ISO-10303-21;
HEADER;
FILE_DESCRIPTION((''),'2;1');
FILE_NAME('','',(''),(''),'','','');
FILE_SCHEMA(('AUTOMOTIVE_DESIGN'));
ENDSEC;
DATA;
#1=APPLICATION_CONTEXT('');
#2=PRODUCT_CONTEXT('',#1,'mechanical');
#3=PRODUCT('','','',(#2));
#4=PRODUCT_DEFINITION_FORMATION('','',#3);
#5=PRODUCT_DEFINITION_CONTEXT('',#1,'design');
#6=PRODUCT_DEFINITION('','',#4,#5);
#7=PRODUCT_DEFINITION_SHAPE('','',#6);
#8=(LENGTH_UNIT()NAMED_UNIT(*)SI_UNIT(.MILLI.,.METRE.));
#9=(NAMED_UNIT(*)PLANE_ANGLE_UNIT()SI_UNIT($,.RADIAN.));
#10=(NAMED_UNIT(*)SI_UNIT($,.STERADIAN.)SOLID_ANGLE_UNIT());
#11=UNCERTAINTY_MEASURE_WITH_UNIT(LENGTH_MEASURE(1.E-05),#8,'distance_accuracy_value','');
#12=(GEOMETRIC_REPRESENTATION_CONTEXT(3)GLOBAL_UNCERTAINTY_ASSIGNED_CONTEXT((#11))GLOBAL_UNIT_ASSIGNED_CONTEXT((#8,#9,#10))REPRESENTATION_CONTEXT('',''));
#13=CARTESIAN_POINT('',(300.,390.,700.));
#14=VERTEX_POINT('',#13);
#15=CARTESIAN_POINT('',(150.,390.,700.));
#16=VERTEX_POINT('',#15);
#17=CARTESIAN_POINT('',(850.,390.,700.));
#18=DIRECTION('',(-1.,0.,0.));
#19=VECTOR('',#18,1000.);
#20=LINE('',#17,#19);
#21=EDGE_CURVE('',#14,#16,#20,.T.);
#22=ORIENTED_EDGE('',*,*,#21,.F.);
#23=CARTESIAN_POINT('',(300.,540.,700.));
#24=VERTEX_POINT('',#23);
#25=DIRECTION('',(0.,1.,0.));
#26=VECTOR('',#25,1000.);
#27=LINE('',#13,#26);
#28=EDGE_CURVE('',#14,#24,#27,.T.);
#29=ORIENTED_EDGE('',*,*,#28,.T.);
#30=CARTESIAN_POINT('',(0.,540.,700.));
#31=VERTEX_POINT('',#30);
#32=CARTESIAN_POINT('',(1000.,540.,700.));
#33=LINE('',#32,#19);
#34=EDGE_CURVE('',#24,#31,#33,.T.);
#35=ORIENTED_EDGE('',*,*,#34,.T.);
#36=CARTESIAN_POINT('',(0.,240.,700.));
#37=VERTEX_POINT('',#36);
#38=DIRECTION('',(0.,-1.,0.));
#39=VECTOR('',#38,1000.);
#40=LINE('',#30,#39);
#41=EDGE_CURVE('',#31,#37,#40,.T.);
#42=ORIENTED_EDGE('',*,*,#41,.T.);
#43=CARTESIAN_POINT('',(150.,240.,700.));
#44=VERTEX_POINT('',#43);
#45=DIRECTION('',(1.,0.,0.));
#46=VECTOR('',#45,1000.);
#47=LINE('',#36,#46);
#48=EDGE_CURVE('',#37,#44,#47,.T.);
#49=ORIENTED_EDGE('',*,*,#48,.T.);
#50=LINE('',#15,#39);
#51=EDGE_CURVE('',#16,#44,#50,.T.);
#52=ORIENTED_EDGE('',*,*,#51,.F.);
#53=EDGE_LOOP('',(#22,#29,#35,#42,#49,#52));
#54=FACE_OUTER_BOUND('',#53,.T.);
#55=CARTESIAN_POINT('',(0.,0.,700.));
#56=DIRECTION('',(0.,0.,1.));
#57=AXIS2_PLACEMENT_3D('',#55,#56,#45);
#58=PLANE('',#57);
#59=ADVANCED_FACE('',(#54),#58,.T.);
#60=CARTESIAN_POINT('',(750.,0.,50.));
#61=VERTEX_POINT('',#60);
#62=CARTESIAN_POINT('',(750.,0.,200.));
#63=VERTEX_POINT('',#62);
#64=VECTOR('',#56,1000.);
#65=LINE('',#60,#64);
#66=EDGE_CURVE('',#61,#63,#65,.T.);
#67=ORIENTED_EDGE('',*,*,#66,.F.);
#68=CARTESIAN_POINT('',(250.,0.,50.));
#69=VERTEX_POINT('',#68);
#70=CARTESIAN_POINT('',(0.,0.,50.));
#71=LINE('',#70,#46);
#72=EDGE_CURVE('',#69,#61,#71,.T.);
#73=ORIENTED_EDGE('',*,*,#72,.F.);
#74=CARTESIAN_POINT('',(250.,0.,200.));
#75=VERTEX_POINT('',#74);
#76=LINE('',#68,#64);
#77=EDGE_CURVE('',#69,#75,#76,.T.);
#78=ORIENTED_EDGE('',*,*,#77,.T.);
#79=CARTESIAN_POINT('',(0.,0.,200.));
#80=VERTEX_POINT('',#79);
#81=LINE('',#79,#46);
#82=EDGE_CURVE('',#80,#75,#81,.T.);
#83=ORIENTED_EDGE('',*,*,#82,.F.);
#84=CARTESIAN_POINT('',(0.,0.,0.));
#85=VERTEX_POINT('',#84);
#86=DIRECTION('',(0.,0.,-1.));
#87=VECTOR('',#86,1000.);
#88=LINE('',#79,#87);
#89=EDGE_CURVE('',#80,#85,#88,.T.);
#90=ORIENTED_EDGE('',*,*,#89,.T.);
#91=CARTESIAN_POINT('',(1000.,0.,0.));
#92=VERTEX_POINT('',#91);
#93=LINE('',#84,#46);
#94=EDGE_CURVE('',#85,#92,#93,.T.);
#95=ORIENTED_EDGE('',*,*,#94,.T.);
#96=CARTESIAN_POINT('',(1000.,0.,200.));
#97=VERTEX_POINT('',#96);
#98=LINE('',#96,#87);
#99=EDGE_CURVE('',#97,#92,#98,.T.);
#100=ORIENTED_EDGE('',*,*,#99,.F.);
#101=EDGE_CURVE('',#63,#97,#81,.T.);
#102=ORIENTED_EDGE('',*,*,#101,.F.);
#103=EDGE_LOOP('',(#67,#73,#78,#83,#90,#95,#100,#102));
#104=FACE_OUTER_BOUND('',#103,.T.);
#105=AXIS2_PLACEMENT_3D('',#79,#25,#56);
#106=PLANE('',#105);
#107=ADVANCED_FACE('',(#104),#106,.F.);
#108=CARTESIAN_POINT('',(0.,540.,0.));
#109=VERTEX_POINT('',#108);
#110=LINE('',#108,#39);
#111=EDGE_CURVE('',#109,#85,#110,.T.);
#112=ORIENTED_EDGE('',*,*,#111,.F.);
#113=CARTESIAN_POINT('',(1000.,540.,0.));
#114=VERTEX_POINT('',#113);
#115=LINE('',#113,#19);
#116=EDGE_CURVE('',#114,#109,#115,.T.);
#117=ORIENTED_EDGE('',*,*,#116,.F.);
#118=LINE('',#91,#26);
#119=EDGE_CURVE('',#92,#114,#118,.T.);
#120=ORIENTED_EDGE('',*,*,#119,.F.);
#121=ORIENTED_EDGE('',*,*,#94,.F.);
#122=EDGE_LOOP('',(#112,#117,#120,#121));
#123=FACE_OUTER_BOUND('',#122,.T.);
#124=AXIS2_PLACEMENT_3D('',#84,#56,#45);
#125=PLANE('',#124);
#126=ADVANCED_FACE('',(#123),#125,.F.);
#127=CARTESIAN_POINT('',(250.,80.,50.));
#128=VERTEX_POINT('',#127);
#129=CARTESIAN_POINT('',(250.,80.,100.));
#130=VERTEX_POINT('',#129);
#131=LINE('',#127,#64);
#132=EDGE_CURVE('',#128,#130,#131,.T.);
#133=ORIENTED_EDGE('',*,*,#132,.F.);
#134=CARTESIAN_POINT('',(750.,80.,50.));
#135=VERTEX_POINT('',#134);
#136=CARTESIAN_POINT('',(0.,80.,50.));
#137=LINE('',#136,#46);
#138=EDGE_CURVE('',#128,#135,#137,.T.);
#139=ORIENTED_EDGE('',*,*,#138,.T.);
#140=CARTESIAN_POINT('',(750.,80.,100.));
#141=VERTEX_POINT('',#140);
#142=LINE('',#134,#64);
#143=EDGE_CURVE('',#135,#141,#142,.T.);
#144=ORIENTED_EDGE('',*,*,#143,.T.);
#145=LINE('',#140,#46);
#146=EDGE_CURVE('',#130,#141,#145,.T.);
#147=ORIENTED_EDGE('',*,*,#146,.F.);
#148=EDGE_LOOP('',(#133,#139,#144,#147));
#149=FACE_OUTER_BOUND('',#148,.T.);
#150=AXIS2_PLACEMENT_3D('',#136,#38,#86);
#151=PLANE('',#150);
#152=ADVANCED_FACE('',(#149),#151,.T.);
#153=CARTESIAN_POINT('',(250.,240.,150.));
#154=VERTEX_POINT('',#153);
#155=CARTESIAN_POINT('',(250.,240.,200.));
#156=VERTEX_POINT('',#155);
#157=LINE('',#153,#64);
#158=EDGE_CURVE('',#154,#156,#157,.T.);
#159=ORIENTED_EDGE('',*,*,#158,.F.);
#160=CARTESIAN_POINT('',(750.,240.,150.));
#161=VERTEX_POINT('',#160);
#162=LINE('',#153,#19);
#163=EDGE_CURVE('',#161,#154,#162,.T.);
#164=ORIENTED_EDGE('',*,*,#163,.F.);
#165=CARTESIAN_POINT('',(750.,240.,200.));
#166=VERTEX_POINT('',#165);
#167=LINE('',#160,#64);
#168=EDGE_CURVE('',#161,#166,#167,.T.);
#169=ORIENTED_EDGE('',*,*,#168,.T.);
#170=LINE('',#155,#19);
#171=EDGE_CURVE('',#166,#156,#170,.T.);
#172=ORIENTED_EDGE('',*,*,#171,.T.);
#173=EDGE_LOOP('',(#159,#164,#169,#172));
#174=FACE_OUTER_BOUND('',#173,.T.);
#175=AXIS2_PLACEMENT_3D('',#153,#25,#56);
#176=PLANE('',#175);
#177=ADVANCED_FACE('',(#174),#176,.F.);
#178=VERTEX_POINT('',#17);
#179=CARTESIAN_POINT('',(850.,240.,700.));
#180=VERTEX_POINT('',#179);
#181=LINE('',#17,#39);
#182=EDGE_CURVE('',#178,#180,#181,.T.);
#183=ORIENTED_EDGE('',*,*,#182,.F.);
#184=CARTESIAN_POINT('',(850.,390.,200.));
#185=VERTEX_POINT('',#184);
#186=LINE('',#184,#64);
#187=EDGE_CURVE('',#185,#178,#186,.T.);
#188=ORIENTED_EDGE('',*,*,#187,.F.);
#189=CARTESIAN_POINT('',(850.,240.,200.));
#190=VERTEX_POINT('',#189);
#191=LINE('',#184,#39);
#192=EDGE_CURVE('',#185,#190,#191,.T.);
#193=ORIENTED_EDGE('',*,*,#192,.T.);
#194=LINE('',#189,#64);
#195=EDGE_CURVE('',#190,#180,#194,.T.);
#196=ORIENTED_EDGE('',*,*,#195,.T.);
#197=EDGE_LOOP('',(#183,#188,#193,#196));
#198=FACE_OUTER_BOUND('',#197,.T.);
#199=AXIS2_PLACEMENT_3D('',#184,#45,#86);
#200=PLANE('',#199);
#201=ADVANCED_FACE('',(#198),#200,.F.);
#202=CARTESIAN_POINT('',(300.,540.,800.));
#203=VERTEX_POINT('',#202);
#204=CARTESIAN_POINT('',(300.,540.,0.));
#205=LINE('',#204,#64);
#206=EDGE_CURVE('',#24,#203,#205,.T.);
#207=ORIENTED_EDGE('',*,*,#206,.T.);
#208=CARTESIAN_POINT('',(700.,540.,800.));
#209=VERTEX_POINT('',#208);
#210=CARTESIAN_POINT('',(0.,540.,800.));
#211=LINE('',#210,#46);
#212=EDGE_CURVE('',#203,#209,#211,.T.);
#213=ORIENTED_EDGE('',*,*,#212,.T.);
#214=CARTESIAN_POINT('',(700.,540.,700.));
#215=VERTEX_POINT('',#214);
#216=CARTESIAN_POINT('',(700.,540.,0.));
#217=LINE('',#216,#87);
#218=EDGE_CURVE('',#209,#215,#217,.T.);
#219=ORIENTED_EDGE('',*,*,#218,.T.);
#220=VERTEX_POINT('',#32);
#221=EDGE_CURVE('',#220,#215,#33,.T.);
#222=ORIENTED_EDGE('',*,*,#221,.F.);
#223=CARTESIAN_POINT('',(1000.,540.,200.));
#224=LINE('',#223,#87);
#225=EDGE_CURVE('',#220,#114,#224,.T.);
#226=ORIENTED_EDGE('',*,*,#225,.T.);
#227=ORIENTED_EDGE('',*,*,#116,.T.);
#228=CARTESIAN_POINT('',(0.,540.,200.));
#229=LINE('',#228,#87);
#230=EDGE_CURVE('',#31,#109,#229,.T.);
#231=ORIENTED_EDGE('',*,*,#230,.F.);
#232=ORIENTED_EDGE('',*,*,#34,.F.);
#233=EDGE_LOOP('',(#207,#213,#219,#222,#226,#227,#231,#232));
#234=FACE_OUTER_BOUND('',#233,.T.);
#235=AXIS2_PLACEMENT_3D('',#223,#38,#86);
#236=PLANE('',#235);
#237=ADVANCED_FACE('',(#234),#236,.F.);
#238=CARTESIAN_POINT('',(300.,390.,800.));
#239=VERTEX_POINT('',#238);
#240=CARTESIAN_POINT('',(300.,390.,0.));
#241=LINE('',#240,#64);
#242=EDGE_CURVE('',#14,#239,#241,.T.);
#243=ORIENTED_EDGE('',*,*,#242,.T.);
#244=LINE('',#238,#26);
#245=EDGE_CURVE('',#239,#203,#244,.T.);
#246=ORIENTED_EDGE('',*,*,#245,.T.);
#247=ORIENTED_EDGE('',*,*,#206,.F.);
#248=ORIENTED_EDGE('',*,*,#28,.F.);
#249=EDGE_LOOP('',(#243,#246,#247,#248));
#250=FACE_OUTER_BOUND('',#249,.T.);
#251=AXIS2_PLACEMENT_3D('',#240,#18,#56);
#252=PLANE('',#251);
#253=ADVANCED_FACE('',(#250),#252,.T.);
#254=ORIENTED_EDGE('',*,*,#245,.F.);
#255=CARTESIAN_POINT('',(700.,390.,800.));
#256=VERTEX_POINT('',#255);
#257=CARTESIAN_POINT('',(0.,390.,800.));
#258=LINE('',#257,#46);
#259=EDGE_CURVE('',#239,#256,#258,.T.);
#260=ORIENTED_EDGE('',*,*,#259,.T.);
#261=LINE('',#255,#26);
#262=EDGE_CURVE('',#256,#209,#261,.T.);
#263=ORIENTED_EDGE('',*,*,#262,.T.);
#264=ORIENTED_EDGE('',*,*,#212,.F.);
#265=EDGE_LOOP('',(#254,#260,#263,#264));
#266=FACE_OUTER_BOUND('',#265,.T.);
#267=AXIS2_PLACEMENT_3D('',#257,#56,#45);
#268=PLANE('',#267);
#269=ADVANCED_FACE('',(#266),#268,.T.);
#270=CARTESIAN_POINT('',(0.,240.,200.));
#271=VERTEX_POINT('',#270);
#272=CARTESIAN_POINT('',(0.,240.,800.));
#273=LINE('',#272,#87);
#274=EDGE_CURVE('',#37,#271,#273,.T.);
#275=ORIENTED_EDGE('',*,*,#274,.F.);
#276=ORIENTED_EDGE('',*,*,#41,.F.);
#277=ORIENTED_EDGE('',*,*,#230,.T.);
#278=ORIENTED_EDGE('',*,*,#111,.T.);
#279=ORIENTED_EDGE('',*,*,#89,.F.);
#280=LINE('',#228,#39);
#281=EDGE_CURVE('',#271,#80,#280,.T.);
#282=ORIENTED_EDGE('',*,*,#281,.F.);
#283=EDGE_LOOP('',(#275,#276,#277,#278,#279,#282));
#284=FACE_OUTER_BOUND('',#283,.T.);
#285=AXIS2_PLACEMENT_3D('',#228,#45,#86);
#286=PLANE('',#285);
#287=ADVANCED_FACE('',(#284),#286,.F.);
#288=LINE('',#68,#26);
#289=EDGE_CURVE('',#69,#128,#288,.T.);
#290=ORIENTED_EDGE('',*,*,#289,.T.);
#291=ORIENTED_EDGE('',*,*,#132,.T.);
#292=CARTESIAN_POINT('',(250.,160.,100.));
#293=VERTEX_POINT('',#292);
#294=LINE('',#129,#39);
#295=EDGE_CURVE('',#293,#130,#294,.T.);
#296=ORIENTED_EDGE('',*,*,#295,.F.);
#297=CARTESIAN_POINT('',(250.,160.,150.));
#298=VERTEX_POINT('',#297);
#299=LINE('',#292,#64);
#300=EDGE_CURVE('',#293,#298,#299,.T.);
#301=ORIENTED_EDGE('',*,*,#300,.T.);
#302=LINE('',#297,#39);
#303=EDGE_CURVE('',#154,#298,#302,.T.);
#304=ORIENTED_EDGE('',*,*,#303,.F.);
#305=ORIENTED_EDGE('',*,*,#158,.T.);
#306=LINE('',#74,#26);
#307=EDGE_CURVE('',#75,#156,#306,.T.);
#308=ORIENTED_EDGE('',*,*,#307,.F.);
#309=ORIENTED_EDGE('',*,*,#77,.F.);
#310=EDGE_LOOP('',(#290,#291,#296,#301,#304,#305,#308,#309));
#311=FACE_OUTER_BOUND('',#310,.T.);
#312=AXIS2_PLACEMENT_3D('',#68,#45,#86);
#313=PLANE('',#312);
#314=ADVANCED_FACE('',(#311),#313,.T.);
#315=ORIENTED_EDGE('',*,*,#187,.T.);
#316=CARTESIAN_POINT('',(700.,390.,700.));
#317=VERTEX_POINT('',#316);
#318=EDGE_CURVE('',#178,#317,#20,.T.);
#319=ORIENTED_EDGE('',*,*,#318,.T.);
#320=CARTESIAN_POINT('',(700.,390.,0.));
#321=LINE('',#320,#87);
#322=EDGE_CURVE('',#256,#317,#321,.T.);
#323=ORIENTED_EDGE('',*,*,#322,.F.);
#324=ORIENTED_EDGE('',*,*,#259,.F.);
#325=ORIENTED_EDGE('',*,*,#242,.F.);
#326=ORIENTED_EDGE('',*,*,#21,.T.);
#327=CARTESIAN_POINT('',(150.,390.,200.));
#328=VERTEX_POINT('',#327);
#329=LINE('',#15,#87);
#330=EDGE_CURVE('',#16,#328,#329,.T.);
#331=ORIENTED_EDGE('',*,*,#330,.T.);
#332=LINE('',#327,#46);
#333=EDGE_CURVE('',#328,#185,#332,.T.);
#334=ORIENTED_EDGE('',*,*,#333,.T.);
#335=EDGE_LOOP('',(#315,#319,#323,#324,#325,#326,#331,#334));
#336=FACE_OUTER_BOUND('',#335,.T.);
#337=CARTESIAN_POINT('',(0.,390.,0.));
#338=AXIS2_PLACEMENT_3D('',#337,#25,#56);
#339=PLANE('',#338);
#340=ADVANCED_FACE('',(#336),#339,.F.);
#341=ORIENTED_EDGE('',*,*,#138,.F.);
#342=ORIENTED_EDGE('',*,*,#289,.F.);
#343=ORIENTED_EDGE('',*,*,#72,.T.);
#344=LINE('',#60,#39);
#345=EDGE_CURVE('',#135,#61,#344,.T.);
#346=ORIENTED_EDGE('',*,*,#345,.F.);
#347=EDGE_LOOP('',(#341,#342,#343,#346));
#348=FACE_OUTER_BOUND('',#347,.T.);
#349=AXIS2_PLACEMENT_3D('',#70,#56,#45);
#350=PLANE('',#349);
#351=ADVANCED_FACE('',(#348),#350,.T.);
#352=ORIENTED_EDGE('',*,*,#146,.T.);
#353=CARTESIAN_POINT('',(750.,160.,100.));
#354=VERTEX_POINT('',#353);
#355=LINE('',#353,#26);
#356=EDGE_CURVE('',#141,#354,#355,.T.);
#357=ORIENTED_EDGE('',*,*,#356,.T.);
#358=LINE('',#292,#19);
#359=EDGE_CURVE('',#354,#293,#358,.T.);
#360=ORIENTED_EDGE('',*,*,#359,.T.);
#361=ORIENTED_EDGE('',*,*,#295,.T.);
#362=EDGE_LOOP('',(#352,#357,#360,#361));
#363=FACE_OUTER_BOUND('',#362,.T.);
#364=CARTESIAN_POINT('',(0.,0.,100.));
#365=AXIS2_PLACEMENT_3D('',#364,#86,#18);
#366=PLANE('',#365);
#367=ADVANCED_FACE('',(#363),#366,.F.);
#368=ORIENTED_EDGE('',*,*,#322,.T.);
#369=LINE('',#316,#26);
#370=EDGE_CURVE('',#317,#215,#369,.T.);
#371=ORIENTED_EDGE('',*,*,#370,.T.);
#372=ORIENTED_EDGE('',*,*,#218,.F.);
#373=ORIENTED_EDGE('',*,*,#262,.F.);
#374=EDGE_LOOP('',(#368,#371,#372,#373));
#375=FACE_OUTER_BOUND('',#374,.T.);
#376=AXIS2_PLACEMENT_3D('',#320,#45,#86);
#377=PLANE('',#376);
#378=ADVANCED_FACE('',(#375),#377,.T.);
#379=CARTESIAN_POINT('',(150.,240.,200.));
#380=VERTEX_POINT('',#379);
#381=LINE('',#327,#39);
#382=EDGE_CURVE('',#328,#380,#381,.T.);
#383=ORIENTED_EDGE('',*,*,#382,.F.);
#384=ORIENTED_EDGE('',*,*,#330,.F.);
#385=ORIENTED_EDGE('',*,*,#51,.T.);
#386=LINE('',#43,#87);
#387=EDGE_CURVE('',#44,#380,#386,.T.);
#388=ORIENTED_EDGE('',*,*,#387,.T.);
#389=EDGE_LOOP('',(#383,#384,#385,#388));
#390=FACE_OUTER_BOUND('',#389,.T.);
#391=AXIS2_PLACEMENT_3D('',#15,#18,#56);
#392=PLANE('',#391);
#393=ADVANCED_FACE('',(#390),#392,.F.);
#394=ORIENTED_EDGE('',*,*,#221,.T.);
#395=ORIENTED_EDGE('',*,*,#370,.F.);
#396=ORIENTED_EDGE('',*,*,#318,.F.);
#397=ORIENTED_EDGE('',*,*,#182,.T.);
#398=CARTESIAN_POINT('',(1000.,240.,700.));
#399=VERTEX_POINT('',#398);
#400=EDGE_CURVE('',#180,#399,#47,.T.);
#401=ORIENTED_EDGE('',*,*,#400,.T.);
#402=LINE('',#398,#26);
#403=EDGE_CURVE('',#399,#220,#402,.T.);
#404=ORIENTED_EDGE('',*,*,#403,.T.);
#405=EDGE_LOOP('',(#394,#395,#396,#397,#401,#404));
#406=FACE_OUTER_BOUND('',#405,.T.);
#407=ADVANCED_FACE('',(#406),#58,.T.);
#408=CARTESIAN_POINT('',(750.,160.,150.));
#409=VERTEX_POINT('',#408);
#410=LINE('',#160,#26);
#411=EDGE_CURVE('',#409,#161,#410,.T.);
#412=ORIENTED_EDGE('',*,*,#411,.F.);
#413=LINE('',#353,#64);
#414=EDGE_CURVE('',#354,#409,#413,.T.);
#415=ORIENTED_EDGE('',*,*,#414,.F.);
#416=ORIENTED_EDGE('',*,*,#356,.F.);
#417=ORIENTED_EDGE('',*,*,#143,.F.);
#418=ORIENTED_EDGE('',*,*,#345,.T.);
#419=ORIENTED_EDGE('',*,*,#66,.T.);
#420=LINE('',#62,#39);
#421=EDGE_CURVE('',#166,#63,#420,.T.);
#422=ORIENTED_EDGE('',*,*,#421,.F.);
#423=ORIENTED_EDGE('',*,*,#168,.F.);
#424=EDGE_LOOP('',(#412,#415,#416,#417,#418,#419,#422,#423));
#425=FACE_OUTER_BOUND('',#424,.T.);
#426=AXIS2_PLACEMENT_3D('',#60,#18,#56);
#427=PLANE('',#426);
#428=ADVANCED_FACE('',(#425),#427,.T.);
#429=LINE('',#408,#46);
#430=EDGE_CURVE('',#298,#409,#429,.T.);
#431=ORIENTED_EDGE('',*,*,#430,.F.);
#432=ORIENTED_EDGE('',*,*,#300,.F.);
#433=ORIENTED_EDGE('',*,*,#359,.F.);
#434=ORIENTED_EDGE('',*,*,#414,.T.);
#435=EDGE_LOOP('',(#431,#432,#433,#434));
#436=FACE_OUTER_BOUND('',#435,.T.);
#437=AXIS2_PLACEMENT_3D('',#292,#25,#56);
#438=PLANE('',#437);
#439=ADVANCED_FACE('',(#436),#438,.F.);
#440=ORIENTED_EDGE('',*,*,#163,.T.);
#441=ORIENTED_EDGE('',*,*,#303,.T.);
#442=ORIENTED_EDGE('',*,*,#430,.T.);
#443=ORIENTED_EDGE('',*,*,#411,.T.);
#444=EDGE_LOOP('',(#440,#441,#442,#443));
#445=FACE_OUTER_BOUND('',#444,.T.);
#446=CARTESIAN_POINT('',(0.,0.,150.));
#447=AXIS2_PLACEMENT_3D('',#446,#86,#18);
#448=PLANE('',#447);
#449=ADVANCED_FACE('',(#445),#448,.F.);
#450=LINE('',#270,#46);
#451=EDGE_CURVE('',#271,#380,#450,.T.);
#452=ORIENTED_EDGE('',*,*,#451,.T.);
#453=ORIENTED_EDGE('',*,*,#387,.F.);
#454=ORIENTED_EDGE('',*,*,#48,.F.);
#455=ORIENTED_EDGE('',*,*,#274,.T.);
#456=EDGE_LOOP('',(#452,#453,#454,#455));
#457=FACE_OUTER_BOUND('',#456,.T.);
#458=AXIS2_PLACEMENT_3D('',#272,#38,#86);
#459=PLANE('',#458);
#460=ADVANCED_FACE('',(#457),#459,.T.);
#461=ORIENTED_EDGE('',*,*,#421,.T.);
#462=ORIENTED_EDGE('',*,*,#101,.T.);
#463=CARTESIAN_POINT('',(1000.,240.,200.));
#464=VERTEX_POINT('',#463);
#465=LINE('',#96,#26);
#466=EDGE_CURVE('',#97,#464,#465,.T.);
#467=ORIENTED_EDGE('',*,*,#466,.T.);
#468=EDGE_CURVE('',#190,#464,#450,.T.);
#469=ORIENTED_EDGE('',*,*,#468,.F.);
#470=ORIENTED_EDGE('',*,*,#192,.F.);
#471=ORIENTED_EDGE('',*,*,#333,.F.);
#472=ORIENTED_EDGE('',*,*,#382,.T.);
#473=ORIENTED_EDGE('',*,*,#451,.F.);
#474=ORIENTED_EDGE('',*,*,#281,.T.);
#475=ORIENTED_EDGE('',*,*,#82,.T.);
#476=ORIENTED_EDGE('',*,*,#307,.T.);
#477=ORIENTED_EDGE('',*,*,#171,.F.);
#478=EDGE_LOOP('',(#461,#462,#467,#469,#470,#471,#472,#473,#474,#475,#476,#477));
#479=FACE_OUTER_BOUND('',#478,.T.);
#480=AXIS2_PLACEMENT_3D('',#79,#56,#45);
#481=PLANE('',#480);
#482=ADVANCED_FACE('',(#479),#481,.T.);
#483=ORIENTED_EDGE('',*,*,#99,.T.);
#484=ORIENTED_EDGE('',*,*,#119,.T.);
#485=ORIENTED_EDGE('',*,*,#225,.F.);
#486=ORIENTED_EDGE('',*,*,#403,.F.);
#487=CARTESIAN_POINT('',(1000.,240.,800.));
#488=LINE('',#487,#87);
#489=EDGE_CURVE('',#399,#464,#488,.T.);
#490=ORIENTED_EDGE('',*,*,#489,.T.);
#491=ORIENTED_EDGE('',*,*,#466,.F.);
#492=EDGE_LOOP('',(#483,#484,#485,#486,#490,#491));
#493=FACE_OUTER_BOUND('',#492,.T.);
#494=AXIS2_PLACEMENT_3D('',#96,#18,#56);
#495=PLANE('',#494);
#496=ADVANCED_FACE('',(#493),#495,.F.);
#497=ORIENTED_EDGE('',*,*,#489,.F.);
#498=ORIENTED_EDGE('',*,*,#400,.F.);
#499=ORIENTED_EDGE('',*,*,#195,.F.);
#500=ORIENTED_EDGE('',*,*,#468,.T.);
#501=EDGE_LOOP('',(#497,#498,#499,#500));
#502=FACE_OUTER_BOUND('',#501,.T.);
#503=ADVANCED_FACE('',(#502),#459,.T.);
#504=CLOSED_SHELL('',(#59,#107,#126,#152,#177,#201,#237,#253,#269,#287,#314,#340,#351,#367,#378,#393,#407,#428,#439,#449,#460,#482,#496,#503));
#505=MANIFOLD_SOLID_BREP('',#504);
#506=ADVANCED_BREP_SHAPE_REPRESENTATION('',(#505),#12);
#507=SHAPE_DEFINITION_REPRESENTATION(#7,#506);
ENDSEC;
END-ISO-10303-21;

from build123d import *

# Parameters (mm, degrees)
BASE_BLOCK_PROFILE_W            = 1000
BASE_BLOCK_PROFILE_H            = 540
BASE_BLOCK_DEPTH                = 200
RAISED_BLOCK_PROFILE_W          = 600
RAISED_BLOCK_PROFILE_H          = 300
RAISED_BLOCK_DEPTH              = 1000
RAISED_BLOCK_STEP_CUT_PROFILE_W = 1000
RAISED_BLOCK_STEP_CUT_PROFILE_H = 300
RAISED_BLOCK_STEP_CUT_DEPTH     = 100
STAIR_STEP_BOSS_PROFILE_W       = 200
STAIR_STEP_BOSS_PROFILE_H       = 100
STAIR_STEP_BOSS_DEPTH           = 150
STAIR_CUTOUT_DEPTH              = 150
STEPPED_SLOT_PROFILE_W          = 250
STEPPED_SLOT_PROFILE_H          = 80
STEPPED_SLOT_CUT_DEPTH          = 150
SLOT_SECOND_STEP_PROFILE_W      = 500
SLOT_SECOND_STEP_PROFILE_H      = 80
SLOT_SECOND_STEP_CUT_DEPTH      = 100
SLOT_THIRD_STEP_PROFILE_W       = 500
SLOT_THIRD_STEP_PROFILE_H       = 80
SLOT_THIRD_STEP_CUT_DEPTH       = 50


with BuildPart() as part:
    # Base Block Profile → Base Block (new body)
    with BuildSketch(Plane.XY):
        with Locations((500, 270)):
            Rectangle(BASE_BLOCK_PROFILE_W, BASE_BLOCK_PROFILE_H)
    extrude(amount=BASE_BLOCK_DEPTH)

    # Raised Block Profile → Raised Block (add)
    with BuildSketch(Plane(origin=(1000, 0, 0), x_dir=(0, 0, -1), z_dir=(1, 0, 0))):
        with Locations((-500, 390)):
            Rectangle(RAISED_BLOCK_PROFILE_W, RAISED_BLOCK_PROFILE_H)
    extrude(amount=-RAISED_BLOCK_DEPTH)

    # Raised Block Step Cut Profile → Raised Block Step Cut (cut)
    with BuildSketch(Plane.XY.offset(800)):
        with Locations((500, 390)):
            Rectangle(RAISED_BLOCK_STEP_CUT_PROFILE_W, RAISED_BLOCK_STEP_CUT_PROFILE_H)
    extrude(amount=-RAISED_BLOCK_STEP_CUT_DEPTH, mode=Mode.SUBTRACT)

    # Stair Step Boss Profile → Stair Step Boss (add)
    with BuildSketch(Plane(origin=(0, 540, 0), x_dir=(1, 0, 0), z_dir=(0, 1, 0))):
        with Locations((400, -750)):
            Rectangle(STAIR_STEP_BOSS_PROFILE_W, STAIR_STEP_BOSS_PROFILE_H)
        with Locations((600, -750)):
            Rectangle(STAIR_STEP_BOSS_PROFILE_W, STAIR_STEP_BOSS_PROFILE_H)
    extrude(amount=-STAIR_STEP_BOSS_DEPTH)

    # Stair Cutout Profile → Stair Cutout (cut)
    with BuildSketch(Plane.XZ.offset(-240)):
        Polygon((500, 700), (150, 700), (150, 200), (850, 200), (850, 700), align=None)
    extrude(amount=-STAIR_CUTOUT_DEPTH, mode=Mode.SUBTRACT)

    # Stepped Slot Profile → Stepped Slot Cut (cut)
    with BuildSketch(Plane.XY.offset(200)):
        with Locations((375, 40)):
            Rectangle(STEPPED_SLOT_PROFILE_W, STEPPED_SLOT_PROFILE_H)
        with Locations((625, 40)):
            Rectangle(STEPPED_SLOT_PROFILE_W, STEPPED_SLOT_PROFILE_H)
    extrude(amount=-STEPPED_SLOT_CUT_DEPTH, mode=Mode.SUBTRACT)

    # Slot Second Step Profile → Slot Second Step Cut (cut)
    with BuildSketch(Plane.XY.offset(200)):
        with Locations((500, 120)):
            Rectangle(SLOT_SECOND_STEP_PROFILE_W, SLOT_SECOND_STEP_PROFILE_H)
    extrude(amount=-SLOT_SECOND_STEP_CUT_DEPTH, mode=Mode.SUBTRACT)

    # Slot Third Step Profile → Slot Third Step Cut (cut)
    with BuildSketch(Plane.XY.offset(200)):
        with Locations((500, 200)):
            Rectangle(SLOT_THIRD_STEP_PROFILE_W, SLOT_THIRD_STEP_PROFILE_H)
    extrude(amount=-SLOT_THIRD_STEP_CUT_DEPTH, mode=Mode.SUBTRACT)


solid = part.part
